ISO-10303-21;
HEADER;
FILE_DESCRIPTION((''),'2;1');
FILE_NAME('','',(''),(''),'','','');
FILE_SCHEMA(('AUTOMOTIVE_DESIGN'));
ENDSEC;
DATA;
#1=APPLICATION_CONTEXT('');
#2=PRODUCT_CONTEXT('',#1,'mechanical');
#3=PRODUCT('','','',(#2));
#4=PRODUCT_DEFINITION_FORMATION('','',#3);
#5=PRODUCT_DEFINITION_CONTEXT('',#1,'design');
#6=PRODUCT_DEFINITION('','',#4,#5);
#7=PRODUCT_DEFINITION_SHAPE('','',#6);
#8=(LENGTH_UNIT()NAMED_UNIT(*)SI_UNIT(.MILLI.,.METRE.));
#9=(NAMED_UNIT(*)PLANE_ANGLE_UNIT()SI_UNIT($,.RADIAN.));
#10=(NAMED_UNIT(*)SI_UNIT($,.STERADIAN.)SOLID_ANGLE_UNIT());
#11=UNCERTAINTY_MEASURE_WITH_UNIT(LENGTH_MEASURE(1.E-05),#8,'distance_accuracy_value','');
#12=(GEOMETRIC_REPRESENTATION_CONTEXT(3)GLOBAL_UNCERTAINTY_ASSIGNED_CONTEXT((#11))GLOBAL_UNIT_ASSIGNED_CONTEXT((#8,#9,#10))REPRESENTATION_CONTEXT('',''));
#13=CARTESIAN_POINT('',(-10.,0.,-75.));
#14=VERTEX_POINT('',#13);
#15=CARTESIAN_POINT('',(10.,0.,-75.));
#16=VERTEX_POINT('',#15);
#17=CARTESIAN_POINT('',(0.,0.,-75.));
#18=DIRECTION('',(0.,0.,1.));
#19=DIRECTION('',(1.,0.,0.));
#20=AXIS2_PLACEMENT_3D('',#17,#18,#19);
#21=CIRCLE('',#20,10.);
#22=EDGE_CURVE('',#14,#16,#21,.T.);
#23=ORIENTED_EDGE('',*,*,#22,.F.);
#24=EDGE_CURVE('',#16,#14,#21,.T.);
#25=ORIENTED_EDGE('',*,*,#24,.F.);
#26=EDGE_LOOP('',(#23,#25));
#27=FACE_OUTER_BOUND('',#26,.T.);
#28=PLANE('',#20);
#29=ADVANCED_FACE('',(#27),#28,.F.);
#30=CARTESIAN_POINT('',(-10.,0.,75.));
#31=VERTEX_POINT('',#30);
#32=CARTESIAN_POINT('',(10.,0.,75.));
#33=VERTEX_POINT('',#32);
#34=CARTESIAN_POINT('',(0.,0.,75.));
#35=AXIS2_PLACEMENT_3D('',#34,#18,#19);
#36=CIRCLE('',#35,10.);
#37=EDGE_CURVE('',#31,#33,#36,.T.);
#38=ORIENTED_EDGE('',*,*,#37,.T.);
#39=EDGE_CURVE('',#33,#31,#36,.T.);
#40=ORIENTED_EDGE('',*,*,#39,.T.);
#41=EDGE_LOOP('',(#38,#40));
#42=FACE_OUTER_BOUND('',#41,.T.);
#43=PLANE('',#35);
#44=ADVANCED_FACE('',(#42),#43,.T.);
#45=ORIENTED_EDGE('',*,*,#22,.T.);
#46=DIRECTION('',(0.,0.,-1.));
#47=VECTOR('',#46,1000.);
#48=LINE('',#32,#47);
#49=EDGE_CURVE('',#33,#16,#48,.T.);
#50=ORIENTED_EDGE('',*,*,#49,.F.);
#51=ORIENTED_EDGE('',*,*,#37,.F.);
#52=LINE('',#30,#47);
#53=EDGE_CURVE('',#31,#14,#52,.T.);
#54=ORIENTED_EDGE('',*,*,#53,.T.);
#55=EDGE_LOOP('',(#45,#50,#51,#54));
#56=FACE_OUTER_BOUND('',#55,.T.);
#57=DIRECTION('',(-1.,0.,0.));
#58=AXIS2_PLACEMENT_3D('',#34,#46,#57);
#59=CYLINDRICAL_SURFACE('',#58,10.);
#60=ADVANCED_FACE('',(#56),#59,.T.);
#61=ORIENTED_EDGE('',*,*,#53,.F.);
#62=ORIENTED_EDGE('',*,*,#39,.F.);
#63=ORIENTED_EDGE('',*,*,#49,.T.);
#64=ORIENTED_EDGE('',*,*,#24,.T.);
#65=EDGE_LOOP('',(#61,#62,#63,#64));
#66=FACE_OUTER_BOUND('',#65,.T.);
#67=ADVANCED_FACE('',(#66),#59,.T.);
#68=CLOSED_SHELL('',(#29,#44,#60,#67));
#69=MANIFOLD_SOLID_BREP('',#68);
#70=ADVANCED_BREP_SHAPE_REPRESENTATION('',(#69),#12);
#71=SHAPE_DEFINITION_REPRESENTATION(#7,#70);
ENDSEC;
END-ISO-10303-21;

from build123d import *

# Parameters (mm, degrees)
SKETCH_1_R      = 10
EXTRUDE_1_DEPTH = 75


with BuildPart() as part:
    # 草图1 → 凸台-拉伸1 (new, symmetric)
    with BuildSketch(Plane.XY):
        Circle(SKETCH_1_R)
    extrude(amount=EXTRUDE_1_DEPTH, both=True)


solid = part.part
